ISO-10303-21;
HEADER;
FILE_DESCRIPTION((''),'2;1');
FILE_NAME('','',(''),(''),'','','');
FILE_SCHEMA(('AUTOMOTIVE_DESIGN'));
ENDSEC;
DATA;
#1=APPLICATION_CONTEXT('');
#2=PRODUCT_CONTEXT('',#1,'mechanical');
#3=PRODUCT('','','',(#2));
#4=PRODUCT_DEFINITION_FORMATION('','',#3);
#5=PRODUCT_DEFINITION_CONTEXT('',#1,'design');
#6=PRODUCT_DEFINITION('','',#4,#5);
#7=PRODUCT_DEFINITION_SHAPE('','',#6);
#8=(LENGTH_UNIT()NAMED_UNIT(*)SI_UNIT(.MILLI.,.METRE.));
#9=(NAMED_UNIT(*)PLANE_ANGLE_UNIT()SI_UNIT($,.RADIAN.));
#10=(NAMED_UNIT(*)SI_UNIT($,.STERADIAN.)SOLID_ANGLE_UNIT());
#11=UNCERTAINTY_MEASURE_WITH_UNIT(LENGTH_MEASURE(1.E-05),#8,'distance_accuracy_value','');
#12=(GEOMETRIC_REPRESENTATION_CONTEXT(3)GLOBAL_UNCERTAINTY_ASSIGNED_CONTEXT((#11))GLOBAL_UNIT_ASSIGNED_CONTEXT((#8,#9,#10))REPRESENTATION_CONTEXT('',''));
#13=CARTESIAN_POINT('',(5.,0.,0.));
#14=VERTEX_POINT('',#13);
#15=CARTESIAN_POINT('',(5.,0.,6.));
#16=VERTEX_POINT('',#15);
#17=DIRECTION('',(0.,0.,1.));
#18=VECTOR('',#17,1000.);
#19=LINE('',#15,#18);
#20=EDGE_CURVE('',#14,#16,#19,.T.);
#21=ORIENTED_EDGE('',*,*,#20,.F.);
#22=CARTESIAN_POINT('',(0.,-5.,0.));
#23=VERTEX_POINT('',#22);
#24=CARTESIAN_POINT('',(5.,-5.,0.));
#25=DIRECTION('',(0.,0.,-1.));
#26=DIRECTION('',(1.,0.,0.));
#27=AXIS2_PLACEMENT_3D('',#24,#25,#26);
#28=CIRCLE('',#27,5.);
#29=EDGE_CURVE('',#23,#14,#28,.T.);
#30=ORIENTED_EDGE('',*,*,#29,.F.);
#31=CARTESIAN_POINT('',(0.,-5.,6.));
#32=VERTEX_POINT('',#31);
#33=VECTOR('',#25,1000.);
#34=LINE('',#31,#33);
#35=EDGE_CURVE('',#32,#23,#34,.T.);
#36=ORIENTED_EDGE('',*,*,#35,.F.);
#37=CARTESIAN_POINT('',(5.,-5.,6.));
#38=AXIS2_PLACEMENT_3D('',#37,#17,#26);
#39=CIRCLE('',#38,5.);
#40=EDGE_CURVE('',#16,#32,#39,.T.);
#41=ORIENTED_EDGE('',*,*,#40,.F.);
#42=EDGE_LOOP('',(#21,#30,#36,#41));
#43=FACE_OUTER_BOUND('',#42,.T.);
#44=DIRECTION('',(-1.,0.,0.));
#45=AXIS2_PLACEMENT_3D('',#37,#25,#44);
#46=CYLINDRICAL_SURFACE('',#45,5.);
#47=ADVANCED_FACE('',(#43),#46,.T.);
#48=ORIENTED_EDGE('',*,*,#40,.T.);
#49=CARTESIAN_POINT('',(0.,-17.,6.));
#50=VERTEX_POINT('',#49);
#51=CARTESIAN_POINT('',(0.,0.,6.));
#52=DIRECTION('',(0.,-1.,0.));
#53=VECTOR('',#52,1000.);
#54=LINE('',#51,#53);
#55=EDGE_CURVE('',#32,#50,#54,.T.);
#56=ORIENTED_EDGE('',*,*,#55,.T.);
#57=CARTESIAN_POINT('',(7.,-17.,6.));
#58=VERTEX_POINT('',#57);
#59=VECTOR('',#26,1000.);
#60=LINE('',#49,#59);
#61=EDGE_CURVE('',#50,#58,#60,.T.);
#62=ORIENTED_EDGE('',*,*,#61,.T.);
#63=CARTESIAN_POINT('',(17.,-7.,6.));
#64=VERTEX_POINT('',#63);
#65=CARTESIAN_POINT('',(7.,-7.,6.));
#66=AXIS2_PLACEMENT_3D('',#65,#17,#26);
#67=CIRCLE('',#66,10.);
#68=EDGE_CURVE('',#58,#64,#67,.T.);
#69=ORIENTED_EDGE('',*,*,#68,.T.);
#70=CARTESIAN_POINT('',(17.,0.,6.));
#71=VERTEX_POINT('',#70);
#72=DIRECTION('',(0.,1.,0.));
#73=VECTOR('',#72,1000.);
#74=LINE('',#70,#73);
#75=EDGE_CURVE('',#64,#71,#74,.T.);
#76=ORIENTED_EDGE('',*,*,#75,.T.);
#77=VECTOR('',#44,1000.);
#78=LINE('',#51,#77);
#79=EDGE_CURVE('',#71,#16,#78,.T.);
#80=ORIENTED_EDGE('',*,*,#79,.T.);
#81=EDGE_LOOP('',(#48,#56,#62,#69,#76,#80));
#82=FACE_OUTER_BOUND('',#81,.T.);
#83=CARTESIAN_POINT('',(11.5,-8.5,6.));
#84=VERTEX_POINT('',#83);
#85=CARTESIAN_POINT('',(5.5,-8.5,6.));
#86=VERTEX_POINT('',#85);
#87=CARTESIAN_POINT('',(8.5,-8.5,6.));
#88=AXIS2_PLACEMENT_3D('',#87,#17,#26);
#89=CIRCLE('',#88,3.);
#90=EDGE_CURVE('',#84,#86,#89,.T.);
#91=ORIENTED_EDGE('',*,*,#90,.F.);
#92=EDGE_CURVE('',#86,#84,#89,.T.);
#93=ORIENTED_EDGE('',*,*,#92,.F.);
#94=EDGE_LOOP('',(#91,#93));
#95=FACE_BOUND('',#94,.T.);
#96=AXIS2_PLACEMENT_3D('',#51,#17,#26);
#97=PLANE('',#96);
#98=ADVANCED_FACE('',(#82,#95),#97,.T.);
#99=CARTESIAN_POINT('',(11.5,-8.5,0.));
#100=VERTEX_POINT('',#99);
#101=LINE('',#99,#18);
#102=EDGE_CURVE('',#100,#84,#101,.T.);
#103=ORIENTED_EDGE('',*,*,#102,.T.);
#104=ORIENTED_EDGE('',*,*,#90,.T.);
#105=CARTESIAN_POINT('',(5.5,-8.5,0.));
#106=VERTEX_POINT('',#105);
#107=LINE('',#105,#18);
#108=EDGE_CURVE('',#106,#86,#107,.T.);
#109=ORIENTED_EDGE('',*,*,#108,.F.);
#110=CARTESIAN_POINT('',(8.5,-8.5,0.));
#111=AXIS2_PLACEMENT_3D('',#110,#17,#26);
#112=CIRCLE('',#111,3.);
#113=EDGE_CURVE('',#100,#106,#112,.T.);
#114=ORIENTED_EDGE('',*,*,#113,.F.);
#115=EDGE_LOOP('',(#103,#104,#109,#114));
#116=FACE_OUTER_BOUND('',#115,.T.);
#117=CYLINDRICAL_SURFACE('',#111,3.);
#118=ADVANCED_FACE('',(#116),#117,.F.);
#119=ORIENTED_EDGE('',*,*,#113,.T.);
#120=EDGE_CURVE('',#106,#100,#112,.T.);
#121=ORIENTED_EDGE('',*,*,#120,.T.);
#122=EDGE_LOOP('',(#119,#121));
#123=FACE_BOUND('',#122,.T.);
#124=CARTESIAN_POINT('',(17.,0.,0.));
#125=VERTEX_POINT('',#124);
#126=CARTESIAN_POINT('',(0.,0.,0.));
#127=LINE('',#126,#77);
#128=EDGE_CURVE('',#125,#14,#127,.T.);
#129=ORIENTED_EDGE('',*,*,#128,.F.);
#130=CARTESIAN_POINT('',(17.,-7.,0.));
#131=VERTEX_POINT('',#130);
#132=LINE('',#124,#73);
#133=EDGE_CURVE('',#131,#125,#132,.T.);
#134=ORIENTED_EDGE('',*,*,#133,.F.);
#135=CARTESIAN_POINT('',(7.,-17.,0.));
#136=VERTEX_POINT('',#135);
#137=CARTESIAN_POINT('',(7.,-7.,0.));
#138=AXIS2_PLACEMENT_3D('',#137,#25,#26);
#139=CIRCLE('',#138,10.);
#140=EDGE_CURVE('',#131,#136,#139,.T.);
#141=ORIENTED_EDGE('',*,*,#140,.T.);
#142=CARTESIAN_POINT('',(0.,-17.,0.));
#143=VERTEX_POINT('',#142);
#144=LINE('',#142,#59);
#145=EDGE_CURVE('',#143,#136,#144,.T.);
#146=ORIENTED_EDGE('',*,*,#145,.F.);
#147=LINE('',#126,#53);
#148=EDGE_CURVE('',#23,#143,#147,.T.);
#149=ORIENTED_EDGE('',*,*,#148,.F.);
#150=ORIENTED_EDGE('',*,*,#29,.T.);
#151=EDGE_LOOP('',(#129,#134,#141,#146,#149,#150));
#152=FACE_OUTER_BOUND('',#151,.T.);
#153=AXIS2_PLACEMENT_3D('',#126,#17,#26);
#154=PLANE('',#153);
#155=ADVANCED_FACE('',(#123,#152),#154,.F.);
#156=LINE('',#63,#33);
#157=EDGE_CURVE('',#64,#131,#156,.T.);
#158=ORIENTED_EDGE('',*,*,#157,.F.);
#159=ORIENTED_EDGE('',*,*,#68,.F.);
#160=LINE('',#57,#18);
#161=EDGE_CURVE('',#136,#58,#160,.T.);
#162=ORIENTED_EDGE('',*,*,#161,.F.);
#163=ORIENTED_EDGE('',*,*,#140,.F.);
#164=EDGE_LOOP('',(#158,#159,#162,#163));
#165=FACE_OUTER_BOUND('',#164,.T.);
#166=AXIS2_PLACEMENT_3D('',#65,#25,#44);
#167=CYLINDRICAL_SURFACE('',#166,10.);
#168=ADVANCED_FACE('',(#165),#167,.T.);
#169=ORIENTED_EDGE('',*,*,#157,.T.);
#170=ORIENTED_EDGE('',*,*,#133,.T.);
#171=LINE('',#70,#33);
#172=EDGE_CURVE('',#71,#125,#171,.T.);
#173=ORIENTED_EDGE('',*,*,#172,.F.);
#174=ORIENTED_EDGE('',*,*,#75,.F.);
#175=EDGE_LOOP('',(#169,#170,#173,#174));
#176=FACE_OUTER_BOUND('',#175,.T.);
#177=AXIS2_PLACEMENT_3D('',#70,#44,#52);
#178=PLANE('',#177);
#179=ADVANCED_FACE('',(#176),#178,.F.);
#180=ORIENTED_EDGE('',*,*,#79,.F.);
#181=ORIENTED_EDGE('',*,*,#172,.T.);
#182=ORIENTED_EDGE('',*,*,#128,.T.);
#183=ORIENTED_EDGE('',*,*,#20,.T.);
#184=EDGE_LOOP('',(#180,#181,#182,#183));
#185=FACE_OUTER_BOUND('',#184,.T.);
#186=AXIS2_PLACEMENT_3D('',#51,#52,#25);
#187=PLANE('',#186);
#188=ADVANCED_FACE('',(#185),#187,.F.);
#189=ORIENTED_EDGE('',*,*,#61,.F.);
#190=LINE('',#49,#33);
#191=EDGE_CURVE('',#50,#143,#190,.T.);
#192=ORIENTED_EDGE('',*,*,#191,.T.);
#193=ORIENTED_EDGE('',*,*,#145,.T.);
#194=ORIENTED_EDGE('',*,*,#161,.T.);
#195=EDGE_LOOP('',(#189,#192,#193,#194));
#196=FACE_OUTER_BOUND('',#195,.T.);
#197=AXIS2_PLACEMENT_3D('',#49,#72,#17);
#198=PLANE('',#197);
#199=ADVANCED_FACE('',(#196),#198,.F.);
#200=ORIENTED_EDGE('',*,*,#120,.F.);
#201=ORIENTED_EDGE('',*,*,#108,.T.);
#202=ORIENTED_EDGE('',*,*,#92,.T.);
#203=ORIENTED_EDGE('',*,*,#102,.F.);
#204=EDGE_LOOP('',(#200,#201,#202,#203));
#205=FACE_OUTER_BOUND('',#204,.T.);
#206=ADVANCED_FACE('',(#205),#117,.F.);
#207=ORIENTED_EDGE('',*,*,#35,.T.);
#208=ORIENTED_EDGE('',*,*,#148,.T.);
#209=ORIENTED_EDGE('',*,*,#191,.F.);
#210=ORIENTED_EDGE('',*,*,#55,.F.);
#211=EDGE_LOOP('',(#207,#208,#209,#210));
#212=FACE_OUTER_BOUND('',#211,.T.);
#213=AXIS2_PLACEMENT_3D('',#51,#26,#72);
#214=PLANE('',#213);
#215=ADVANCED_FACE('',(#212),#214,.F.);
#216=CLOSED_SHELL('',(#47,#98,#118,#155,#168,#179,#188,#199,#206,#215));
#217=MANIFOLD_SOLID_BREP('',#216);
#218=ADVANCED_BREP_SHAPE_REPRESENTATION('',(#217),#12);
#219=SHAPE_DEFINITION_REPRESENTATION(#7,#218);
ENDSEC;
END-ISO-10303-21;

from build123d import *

# Parameters (mm, degrees)
SKETCH1_W           = 17
SKETCH1_H           = 17
BOSS_EXTRUDE1_DEPTH = 6
FILLET1_R           = 10
FILLET2_R           = 5
SKETCH2_R           = 3
CUT_EXTRUDE1_DEPTH  = 6


with BuildPart() as part:
    # Sketch1 → Boss-Extrude1 (new body)
    with BuildSketch(Plane.XY):
        with Locations((8.5, -8.5)):
            Rectangle(SKETCH1_W, SKETCH1_H)
    extrude(amount=BOSS_EXTRUDE1_DEPTH)

    # Fillet1
    fillet1_edges = [part.edges().sort_by_distance(p)[0] for p in [
        (17, -17, 3),
    ]]
    fillet(fillet1_edges, radius=FILLET1_R)

    # Fillet2
    fillet2_edges = [part.edges().sort_by_distance(p)[0] for p in [
        (0, 0, 3),
    ]]
    fillet(fillet2_edges, radius=FILLET2_R)

    # Sketch2 → Cut-Extrude1 (cut)
    with BuildSketch(Plane.XY.offset(6)):
        with Locations((8.5, -8.5)):
            Circle(SKETCH2_R)
    extrude(amount=-CUT_EXTRUDE1_DEPTH, mode=Mode.SUBTRACT)


solid = part.part
